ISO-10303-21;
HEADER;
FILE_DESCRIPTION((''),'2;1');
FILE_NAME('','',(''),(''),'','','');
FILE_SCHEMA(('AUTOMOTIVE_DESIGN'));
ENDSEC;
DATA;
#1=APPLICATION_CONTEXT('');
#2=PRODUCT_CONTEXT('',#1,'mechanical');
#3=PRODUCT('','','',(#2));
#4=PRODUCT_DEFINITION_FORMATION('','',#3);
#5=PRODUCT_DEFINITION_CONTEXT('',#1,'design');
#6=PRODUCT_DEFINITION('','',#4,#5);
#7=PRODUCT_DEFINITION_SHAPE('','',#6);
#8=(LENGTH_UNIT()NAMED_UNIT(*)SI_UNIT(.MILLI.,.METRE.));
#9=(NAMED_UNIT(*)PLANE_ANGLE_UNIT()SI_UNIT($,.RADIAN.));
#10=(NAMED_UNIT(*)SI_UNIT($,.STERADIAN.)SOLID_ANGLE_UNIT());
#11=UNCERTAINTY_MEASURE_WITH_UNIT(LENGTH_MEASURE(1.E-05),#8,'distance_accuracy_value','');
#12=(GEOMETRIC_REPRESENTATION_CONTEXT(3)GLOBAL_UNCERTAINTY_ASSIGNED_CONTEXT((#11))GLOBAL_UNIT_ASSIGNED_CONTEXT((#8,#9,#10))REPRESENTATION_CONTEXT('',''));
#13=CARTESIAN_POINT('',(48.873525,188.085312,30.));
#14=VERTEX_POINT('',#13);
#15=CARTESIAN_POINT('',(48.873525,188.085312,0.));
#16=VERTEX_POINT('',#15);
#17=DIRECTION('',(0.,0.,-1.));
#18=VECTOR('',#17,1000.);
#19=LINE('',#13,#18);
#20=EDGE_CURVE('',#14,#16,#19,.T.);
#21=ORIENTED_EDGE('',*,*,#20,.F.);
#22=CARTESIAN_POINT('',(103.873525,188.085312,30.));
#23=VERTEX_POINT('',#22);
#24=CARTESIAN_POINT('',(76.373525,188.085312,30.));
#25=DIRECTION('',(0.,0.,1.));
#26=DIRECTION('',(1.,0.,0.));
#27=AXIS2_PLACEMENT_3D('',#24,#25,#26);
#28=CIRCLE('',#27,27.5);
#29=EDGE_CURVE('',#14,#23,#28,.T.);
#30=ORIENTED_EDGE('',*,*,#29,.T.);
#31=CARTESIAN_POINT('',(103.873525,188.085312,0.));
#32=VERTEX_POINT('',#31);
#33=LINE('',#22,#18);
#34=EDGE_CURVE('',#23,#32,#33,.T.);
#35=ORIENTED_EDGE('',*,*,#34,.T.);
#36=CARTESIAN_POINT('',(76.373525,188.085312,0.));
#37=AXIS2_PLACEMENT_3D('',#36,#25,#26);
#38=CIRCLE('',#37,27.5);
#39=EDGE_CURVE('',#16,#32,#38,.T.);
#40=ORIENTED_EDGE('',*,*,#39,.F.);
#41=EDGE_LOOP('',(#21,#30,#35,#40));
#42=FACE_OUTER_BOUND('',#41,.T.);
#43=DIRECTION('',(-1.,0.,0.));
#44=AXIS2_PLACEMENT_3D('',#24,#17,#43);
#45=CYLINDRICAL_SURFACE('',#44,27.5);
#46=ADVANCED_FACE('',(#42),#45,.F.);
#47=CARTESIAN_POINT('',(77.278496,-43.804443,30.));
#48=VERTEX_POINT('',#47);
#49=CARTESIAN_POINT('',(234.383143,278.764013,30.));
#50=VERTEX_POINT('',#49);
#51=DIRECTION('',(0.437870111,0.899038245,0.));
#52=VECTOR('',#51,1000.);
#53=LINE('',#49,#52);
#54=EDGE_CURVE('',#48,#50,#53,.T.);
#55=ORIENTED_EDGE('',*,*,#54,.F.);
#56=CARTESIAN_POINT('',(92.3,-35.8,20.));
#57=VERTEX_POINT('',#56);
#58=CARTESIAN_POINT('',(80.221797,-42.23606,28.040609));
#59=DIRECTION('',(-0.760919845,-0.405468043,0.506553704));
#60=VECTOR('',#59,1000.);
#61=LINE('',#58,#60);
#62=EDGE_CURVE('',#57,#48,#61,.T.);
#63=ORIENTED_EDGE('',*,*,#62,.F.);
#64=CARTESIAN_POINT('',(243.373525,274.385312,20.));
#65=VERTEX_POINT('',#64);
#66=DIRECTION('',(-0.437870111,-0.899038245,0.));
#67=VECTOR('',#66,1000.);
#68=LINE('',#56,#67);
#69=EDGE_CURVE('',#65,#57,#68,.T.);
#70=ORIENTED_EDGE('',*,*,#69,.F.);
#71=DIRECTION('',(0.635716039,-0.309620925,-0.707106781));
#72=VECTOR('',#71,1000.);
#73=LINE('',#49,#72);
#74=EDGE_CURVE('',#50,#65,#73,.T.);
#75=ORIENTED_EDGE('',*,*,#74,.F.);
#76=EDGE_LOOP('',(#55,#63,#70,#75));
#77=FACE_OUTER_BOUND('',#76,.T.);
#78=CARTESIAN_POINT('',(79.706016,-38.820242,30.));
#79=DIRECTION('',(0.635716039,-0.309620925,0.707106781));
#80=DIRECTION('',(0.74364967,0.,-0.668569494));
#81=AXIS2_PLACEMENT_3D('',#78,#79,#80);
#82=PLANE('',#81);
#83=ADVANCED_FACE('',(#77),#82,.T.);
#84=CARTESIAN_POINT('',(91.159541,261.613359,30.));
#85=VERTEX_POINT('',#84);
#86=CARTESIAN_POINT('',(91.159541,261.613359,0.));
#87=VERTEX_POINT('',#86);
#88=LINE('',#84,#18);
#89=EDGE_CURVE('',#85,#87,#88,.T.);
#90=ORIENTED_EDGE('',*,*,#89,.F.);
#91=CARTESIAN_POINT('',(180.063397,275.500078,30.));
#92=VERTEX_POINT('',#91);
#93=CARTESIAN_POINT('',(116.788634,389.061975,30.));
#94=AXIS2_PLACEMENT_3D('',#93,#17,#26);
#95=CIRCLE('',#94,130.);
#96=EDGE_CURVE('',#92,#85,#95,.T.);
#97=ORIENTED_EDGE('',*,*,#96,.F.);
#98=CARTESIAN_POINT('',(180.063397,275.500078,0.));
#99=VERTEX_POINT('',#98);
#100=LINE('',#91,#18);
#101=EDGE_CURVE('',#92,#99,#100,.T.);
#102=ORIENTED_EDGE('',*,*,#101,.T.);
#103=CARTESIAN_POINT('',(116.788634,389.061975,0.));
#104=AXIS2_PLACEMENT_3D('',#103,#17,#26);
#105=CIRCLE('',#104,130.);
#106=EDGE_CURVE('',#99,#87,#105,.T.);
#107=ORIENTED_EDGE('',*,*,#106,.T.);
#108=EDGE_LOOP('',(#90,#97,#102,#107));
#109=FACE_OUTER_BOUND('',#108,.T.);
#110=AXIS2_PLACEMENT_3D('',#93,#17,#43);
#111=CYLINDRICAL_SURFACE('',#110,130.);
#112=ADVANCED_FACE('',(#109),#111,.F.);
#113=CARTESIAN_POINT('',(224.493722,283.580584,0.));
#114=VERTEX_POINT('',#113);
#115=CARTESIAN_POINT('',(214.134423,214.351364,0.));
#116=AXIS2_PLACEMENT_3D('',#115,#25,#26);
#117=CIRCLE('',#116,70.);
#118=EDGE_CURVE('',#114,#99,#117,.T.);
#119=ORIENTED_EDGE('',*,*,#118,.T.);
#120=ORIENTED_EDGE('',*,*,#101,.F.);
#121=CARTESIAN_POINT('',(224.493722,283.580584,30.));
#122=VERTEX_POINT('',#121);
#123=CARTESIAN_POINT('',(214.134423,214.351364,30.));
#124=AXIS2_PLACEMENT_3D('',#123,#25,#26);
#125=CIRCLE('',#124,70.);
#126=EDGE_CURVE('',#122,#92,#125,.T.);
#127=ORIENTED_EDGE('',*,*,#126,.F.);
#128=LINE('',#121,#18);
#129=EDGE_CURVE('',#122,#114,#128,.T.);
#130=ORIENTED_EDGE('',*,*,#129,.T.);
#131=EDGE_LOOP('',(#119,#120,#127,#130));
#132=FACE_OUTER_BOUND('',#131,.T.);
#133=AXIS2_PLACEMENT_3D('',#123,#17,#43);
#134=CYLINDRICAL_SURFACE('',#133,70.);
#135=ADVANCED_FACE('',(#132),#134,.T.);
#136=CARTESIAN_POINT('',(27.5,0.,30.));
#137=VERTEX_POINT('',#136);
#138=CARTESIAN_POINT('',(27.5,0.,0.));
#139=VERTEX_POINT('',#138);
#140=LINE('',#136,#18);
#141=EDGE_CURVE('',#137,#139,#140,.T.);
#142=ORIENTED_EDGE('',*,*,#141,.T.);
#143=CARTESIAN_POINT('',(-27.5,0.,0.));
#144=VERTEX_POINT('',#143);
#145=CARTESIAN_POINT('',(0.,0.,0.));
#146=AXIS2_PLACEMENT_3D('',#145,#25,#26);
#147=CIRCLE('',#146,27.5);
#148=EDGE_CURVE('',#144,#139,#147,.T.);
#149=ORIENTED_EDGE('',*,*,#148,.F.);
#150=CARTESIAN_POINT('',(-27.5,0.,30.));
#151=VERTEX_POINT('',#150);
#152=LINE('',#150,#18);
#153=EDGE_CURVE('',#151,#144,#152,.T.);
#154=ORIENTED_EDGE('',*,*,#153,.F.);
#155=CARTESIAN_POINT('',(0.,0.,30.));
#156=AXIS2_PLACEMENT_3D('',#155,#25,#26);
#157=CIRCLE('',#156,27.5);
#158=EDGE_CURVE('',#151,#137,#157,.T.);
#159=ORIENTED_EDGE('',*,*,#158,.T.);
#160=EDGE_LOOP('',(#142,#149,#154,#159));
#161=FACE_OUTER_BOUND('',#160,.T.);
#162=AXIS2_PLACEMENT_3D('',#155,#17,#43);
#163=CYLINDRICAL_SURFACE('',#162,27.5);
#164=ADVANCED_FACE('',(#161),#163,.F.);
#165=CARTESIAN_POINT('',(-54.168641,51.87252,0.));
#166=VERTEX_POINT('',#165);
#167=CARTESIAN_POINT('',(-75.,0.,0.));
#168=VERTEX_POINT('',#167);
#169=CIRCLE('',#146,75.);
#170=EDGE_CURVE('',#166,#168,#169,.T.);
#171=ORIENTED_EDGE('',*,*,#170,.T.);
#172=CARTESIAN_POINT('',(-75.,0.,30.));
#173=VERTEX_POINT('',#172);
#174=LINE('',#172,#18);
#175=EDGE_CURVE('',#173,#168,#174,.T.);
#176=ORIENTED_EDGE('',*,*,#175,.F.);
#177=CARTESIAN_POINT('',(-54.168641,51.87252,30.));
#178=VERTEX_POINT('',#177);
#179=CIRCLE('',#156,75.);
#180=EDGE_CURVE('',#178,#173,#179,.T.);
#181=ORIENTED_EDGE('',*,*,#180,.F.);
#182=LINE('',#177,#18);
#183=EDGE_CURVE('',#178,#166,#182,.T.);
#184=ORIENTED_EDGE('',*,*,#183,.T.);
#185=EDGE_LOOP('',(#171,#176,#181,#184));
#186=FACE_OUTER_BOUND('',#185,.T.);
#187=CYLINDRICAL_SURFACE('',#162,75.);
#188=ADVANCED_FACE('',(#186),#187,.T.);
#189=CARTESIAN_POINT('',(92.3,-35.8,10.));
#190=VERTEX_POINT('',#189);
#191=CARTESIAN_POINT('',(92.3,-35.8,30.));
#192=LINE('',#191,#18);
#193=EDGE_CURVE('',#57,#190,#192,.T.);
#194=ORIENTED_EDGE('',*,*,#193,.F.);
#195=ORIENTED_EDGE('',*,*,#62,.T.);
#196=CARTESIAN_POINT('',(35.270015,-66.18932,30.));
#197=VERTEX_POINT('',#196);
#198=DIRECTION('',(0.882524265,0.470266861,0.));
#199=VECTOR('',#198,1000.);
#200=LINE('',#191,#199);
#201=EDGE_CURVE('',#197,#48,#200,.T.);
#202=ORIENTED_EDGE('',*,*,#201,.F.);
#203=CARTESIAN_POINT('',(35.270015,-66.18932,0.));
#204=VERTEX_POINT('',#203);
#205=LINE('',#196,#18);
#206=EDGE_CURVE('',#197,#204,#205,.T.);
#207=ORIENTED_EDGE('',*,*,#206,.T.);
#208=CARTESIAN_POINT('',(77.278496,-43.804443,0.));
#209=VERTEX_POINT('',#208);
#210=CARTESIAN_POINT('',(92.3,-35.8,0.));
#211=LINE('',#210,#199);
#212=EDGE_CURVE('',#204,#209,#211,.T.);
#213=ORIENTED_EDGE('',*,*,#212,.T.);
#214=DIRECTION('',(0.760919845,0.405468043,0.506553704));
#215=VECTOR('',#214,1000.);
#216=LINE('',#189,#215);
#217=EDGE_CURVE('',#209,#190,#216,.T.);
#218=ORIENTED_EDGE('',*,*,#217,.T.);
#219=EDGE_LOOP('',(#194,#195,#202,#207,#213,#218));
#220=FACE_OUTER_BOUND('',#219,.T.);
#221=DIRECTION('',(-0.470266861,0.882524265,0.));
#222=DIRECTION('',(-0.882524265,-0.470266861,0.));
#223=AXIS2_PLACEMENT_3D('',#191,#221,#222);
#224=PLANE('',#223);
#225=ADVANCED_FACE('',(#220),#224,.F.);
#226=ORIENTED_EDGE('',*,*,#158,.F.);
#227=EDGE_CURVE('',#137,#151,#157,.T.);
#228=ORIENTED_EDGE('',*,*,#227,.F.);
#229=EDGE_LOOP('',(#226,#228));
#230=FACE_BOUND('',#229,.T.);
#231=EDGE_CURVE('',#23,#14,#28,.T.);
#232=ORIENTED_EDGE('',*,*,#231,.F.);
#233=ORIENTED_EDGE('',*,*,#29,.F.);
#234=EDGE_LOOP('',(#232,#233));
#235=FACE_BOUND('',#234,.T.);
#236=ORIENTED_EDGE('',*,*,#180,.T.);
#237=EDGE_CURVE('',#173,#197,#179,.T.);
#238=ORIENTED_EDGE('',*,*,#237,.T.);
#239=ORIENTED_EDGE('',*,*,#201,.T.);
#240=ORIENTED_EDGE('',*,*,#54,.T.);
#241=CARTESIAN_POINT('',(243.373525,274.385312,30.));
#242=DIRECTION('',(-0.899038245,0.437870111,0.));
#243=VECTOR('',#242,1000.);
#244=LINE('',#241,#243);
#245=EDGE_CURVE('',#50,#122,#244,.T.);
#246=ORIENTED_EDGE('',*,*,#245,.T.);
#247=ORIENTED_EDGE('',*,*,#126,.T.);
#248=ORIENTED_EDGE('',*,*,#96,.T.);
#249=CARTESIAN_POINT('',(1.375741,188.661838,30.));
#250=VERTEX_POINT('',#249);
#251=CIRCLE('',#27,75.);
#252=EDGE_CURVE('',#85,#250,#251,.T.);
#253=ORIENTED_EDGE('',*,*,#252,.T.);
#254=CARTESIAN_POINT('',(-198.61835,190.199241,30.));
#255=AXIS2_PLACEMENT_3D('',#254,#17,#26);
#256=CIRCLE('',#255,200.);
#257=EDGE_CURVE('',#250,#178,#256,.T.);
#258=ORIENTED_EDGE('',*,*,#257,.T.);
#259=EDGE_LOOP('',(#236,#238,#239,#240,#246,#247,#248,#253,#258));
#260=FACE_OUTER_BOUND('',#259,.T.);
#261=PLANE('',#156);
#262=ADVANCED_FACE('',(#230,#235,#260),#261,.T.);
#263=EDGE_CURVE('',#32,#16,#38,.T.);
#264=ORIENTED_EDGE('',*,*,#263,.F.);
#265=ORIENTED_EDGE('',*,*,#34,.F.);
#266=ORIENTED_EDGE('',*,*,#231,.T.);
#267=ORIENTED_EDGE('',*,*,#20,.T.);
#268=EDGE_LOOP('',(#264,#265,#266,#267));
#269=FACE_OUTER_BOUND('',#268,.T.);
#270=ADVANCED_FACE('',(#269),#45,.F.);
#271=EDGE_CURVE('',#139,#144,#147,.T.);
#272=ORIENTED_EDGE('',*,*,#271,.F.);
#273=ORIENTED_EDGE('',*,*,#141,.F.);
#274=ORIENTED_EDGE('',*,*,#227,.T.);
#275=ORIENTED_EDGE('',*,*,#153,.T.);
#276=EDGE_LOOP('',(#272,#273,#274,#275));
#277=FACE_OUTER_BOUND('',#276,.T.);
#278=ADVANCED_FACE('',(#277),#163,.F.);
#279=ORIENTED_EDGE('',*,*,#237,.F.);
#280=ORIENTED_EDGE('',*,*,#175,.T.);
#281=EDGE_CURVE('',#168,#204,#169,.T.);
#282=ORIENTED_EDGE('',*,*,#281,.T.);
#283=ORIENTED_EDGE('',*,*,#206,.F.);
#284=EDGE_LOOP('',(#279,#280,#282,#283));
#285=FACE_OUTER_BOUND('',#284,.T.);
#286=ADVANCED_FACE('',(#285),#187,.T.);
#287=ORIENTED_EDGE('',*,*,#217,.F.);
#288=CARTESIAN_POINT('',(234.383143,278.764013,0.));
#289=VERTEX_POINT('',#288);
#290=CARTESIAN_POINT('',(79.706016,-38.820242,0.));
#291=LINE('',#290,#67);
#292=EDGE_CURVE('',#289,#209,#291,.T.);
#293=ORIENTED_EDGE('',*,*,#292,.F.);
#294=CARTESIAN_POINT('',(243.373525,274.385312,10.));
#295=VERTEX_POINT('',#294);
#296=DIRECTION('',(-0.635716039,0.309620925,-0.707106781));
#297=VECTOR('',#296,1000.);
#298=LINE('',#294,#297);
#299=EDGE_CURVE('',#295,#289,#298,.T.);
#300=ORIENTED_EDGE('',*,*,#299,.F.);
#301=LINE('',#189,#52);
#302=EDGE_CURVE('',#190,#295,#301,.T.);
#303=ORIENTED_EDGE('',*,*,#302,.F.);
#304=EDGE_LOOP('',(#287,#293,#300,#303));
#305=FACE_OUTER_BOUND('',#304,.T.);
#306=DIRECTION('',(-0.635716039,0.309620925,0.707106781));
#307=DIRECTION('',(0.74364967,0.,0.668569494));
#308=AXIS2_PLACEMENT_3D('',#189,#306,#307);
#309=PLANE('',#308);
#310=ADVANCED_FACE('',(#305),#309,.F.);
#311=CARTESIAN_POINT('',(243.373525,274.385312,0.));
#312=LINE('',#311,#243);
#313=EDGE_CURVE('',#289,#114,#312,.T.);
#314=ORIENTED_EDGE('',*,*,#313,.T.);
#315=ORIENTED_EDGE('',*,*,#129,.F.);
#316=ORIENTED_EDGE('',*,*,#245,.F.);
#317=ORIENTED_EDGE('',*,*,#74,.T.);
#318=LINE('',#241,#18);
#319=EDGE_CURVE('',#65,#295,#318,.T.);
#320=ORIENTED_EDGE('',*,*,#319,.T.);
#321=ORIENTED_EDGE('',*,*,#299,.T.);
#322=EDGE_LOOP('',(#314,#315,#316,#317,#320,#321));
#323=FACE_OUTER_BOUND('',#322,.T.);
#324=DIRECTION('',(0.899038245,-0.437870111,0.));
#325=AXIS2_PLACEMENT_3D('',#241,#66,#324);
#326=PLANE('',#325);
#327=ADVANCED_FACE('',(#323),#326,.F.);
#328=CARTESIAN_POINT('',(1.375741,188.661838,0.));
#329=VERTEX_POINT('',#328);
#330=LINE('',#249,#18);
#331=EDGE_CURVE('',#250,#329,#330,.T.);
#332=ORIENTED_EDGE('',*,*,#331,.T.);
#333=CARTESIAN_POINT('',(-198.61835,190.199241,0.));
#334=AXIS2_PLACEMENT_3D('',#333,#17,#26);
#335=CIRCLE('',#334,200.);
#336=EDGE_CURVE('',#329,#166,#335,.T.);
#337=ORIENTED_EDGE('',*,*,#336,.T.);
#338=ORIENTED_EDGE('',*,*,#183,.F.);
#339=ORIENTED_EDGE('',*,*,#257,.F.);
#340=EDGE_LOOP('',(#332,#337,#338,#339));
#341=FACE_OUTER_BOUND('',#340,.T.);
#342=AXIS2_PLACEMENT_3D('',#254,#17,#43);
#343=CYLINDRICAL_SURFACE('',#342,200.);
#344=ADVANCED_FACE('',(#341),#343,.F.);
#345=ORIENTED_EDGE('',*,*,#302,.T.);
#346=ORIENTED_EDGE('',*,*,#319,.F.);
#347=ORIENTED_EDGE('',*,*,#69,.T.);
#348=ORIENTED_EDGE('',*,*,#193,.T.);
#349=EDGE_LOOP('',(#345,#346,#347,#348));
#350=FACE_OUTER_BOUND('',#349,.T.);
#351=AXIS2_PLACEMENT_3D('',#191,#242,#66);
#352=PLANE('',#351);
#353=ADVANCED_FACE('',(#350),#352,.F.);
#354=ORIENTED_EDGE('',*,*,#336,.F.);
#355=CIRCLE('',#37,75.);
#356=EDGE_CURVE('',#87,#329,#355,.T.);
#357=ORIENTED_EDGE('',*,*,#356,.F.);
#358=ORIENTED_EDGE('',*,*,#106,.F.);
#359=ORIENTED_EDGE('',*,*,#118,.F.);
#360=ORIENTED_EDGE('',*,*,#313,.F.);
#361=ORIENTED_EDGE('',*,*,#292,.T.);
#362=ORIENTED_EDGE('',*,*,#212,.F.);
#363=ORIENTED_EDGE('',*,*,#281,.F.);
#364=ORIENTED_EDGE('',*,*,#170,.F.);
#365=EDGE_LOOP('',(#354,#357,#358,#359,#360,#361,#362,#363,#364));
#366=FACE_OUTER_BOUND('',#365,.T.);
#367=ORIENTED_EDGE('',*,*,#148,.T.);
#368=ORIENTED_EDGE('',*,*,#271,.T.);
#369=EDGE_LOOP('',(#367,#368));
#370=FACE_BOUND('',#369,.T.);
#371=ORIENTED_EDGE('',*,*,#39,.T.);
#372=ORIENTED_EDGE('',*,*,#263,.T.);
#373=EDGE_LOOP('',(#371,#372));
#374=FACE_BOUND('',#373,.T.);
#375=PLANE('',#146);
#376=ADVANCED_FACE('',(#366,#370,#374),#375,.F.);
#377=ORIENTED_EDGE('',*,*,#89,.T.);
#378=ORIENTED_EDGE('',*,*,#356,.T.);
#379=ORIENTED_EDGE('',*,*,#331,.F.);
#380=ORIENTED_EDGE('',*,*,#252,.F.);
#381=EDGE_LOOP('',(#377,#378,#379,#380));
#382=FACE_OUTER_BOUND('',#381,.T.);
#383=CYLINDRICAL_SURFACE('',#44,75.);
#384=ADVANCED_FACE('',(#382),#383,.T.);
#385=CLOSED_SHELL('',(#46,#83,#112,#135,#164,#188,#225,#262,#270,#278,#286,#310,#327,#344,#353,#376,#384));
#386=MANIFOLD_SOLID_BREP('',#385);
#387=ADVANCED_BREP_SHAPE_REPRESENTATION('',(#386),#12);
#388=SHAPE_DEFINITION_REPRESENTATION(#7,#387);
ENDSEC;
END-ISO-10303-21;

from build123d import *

# Parameters (mm, degrees)
SKETCH1_R           = 27.5
BOSS_EXTRUDE1_DEPTH = 30
CHAMFER1_SIZE       = 10


with BuildPart() as part:
    # Sketch1 → Boss-Extrude1 (new body)
    with BuildSketch(Plane.XY):
        with BuildLine():
            Line((92.3, -35.8), (243.373525417, 274.385312067))
            Line((243.373525417, 274.385312067), (224.493722277, 283.580584405))
            ThreePointArc((224.493722277, 283.580584405), (201.609043027, 283.221639878), (180.06339689, 275.500077984))
            ThreePointArc((180.06339689, 275.500077984), (136.851269704, 260.619417011), (91.159540852, 261.61335942))
            ThreePointArc((91.159540852, 261.61335942), (29.078225578, 246.293169038), (1.375741332, 188.661838097))
            ThreePointArc((1.375741332, 188.661838097), (-13.312623389, 114.954388214), (-54.16864079, 51.87252023))
            ThreePointArc((-54.16864079, 51.87252023), (-59.782430884, -45.288640491), (35.270014595, -66.189319912))
            Line((35.270014595, -66.189319912), (92.3, -35.8))
        make_face()
        with Locations((76.373525417, 188.085312067)):
            Circle(SKETCH1_R, mode=Mode.SUBTRACT)
        Circle(SKETCH1_R, mode=Mode.SUBTRACT)
    extrude(amount=BOSS_EXTRUDE1_DEPTH)

    # Chamfer1
    chamfer1_edges = [part.edges().sort_by_distance(p)[0] for p in [
        (167.836762709, 119.292656033, 0),
        (167.836762709, 119.292656033, 30),
    ]]
    chamfer(chamfer1_edges, length=CHAMFER1_SIZE)


solid = part.part
